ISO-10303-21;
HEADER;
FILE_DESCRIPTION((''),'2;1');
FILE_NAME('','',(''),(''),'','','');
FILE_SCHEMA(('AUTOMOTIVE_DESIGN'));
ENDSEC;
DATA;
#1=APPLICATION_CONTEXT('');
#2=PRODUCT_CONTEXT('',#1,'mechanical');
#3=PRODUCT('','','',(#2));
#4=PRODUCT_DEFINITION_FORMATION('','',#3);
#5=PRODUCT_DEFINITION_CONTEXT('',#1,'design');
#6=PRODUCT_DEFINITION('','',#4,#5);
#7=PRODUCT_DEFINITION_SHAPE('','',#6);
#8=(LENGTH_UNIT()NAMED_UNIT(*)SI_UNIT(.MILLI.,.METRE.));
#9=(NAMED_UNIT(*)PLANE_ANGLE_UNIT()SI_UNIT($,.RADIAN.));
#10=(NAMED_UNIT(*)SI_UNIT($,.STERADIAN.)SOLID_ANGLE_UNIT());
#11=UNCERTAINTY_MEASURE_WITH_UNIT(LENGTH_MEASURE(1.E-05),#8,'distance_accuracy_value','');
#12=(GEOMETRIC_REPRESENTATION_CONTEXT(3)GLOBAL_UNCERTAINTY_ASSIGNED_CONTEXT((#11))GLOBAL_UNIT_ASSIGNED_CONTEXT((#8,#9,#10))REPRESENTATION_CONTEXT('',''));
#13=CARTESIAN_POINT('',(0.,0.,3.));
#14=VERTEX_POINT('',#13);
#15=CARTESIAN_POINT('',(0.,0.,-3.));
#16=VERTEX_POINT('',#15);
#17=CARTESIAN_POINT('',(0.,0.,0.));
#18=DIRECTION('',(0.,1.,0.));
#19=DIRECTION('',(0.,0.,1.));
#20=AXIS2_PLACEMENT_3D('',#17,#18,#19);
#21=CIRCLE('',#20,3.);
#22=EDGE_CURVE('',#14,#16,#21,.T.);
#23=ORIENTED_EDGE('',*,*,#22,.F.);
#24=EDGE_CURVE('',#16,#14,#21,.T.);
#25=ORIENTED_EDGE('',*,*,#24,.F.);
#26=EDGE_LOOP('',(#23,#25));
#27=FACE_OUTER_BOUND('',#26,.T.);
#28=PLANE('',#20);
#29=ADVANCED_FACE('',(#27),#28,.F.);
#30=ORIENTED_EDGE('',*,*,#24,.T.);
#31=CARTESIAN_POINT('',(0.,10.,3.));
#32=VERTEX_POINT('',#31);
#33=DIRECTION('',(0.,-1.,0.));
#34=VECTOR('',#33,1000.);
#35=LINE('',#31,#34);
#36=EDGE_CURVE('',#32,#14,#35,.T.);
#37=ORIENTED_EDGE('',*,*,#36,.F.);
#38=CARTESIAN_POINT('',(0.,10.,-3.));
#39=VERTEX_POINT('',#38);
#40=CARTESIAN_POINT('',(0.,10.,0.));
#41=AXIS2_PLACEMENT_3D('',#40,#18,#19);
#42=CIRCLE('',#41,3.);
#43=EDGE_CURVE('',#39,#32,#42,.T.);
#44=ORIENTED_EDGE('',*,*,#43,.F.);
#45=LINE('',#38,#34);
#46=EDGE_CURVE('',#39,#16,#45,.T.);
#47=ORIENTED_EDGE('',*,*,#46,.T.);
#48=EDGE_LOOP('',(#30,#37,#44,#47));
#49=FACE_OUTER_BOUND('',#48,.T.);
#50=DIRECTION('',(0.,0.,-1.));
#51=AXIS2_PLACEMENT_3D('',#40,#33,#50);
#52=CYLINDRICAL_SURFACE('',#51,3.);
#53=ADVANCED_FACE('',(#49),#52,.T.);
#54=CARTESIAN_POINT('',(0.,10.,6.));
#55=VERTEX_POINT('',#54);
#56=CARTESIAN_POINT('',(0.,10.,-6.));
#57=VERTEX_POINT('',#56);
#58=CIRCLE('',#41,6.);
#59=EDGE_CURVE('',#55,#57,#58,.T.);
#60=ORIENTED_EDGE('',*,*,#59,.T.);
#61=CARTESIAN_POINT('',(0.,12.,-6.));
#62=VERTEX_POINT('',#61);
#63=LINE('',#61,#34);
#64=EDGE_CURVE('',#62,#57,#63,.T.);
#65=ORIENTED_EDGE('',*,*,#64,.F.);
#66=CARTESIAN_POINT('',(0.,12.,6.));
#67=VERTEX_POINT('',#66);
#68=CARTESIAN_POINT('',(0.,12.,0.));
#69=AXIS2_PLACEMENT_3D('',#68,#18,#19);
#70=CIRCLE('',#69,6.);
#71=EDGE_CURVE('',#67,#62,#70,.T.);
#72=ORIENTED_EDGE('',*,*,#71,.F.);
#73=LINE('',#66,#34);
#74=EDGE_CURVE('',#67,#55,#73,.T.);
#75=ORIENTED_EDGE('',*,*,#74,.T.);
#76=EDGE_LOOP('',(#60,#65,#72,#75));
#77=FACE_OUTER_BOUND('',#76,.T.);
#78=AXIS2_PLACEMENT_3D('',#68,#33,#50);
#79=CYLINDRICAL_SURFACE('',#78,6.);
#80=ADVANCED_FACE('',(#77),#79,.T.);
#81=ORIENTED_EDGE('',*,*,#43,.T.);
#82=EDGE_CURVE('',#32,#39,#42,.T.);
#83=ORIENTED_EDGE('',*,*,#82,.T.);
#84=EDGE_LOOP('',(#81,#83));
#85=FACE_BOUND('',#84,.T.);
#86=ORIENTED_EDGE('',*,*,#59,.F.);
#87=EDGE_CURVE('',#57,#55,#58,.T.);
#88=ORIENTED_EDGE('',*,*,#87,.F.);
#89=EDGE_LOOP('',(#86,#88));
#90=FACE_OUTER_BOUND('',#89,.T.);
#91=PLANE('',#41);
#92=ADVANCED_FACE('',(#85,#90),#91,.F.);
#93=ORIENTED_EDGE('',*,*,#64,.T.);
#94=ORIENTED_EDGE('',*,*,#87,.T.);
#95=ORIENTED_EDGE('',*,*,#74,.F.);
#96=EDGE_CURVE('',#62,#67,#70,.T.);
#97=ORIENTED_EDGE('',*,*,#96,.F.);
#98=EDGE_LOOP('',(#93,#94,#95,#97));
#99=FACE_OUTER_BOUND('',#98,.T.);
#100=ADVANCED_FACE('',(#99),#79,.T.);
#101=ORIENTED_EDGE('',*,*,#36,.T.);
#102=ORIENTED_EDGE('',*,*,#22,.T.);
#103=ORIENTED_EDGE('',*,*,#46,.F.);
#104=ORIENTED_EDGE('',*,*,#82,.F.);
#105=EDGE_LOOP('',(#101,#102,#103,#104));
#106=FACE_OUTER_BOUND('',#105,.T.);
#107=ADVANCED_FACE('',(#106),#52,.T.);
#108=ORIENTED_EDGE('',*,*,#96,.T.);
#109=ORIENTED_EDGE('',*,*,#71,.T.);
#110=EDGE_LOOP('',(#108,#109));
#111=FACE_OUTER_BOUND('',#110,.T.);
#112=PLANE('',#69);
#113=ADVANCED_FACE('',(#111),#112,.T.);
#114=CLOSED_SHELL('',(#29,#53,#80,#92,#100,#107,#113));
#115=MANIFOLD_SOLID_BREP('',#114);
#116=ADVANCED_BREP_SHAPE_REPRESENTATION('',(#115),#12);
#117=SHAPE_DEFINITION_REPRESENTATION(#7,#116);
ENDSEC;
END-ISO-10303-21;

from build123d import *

# Parameters (mm, degrees)
SHANK_PROFILE_6_R = 3
SHANK_6X10_DEPTH  = 10
HEAD_PROFILE_12_R = 6
HEAD_12X2_DEPTH   = 2


with BuildPart() as part:
    # Shank Profile Ø6 → Shank Ø6x10 (new body)
    with BuildSketch(Plane(origin=(0, 0, 0), x_dir=(1, 0, 0), z_dir=(0, 1, 0))):
        with Locations(Location((0, 0, 0), (0, 0, 270))):
            Circle(SHANK_PROFILE_6_R)
    extrude(amount=SHANK_6X10_DEPTH)

    # Head Profile Ø12 → Head Ø12x2 (add)
    with BuildSketch(Plane(origin=(0, 10, 0), x_dir=(1, 0, 0), z_dir=(0, 1, 0))):
        with Locations(Location((0, 0, 0), (0, 0, 270))):
            Circle(HEAD_PROFILE_12_R)
    extrude(amount=HEAD_12X2_DEPTH)


solid = part.part
